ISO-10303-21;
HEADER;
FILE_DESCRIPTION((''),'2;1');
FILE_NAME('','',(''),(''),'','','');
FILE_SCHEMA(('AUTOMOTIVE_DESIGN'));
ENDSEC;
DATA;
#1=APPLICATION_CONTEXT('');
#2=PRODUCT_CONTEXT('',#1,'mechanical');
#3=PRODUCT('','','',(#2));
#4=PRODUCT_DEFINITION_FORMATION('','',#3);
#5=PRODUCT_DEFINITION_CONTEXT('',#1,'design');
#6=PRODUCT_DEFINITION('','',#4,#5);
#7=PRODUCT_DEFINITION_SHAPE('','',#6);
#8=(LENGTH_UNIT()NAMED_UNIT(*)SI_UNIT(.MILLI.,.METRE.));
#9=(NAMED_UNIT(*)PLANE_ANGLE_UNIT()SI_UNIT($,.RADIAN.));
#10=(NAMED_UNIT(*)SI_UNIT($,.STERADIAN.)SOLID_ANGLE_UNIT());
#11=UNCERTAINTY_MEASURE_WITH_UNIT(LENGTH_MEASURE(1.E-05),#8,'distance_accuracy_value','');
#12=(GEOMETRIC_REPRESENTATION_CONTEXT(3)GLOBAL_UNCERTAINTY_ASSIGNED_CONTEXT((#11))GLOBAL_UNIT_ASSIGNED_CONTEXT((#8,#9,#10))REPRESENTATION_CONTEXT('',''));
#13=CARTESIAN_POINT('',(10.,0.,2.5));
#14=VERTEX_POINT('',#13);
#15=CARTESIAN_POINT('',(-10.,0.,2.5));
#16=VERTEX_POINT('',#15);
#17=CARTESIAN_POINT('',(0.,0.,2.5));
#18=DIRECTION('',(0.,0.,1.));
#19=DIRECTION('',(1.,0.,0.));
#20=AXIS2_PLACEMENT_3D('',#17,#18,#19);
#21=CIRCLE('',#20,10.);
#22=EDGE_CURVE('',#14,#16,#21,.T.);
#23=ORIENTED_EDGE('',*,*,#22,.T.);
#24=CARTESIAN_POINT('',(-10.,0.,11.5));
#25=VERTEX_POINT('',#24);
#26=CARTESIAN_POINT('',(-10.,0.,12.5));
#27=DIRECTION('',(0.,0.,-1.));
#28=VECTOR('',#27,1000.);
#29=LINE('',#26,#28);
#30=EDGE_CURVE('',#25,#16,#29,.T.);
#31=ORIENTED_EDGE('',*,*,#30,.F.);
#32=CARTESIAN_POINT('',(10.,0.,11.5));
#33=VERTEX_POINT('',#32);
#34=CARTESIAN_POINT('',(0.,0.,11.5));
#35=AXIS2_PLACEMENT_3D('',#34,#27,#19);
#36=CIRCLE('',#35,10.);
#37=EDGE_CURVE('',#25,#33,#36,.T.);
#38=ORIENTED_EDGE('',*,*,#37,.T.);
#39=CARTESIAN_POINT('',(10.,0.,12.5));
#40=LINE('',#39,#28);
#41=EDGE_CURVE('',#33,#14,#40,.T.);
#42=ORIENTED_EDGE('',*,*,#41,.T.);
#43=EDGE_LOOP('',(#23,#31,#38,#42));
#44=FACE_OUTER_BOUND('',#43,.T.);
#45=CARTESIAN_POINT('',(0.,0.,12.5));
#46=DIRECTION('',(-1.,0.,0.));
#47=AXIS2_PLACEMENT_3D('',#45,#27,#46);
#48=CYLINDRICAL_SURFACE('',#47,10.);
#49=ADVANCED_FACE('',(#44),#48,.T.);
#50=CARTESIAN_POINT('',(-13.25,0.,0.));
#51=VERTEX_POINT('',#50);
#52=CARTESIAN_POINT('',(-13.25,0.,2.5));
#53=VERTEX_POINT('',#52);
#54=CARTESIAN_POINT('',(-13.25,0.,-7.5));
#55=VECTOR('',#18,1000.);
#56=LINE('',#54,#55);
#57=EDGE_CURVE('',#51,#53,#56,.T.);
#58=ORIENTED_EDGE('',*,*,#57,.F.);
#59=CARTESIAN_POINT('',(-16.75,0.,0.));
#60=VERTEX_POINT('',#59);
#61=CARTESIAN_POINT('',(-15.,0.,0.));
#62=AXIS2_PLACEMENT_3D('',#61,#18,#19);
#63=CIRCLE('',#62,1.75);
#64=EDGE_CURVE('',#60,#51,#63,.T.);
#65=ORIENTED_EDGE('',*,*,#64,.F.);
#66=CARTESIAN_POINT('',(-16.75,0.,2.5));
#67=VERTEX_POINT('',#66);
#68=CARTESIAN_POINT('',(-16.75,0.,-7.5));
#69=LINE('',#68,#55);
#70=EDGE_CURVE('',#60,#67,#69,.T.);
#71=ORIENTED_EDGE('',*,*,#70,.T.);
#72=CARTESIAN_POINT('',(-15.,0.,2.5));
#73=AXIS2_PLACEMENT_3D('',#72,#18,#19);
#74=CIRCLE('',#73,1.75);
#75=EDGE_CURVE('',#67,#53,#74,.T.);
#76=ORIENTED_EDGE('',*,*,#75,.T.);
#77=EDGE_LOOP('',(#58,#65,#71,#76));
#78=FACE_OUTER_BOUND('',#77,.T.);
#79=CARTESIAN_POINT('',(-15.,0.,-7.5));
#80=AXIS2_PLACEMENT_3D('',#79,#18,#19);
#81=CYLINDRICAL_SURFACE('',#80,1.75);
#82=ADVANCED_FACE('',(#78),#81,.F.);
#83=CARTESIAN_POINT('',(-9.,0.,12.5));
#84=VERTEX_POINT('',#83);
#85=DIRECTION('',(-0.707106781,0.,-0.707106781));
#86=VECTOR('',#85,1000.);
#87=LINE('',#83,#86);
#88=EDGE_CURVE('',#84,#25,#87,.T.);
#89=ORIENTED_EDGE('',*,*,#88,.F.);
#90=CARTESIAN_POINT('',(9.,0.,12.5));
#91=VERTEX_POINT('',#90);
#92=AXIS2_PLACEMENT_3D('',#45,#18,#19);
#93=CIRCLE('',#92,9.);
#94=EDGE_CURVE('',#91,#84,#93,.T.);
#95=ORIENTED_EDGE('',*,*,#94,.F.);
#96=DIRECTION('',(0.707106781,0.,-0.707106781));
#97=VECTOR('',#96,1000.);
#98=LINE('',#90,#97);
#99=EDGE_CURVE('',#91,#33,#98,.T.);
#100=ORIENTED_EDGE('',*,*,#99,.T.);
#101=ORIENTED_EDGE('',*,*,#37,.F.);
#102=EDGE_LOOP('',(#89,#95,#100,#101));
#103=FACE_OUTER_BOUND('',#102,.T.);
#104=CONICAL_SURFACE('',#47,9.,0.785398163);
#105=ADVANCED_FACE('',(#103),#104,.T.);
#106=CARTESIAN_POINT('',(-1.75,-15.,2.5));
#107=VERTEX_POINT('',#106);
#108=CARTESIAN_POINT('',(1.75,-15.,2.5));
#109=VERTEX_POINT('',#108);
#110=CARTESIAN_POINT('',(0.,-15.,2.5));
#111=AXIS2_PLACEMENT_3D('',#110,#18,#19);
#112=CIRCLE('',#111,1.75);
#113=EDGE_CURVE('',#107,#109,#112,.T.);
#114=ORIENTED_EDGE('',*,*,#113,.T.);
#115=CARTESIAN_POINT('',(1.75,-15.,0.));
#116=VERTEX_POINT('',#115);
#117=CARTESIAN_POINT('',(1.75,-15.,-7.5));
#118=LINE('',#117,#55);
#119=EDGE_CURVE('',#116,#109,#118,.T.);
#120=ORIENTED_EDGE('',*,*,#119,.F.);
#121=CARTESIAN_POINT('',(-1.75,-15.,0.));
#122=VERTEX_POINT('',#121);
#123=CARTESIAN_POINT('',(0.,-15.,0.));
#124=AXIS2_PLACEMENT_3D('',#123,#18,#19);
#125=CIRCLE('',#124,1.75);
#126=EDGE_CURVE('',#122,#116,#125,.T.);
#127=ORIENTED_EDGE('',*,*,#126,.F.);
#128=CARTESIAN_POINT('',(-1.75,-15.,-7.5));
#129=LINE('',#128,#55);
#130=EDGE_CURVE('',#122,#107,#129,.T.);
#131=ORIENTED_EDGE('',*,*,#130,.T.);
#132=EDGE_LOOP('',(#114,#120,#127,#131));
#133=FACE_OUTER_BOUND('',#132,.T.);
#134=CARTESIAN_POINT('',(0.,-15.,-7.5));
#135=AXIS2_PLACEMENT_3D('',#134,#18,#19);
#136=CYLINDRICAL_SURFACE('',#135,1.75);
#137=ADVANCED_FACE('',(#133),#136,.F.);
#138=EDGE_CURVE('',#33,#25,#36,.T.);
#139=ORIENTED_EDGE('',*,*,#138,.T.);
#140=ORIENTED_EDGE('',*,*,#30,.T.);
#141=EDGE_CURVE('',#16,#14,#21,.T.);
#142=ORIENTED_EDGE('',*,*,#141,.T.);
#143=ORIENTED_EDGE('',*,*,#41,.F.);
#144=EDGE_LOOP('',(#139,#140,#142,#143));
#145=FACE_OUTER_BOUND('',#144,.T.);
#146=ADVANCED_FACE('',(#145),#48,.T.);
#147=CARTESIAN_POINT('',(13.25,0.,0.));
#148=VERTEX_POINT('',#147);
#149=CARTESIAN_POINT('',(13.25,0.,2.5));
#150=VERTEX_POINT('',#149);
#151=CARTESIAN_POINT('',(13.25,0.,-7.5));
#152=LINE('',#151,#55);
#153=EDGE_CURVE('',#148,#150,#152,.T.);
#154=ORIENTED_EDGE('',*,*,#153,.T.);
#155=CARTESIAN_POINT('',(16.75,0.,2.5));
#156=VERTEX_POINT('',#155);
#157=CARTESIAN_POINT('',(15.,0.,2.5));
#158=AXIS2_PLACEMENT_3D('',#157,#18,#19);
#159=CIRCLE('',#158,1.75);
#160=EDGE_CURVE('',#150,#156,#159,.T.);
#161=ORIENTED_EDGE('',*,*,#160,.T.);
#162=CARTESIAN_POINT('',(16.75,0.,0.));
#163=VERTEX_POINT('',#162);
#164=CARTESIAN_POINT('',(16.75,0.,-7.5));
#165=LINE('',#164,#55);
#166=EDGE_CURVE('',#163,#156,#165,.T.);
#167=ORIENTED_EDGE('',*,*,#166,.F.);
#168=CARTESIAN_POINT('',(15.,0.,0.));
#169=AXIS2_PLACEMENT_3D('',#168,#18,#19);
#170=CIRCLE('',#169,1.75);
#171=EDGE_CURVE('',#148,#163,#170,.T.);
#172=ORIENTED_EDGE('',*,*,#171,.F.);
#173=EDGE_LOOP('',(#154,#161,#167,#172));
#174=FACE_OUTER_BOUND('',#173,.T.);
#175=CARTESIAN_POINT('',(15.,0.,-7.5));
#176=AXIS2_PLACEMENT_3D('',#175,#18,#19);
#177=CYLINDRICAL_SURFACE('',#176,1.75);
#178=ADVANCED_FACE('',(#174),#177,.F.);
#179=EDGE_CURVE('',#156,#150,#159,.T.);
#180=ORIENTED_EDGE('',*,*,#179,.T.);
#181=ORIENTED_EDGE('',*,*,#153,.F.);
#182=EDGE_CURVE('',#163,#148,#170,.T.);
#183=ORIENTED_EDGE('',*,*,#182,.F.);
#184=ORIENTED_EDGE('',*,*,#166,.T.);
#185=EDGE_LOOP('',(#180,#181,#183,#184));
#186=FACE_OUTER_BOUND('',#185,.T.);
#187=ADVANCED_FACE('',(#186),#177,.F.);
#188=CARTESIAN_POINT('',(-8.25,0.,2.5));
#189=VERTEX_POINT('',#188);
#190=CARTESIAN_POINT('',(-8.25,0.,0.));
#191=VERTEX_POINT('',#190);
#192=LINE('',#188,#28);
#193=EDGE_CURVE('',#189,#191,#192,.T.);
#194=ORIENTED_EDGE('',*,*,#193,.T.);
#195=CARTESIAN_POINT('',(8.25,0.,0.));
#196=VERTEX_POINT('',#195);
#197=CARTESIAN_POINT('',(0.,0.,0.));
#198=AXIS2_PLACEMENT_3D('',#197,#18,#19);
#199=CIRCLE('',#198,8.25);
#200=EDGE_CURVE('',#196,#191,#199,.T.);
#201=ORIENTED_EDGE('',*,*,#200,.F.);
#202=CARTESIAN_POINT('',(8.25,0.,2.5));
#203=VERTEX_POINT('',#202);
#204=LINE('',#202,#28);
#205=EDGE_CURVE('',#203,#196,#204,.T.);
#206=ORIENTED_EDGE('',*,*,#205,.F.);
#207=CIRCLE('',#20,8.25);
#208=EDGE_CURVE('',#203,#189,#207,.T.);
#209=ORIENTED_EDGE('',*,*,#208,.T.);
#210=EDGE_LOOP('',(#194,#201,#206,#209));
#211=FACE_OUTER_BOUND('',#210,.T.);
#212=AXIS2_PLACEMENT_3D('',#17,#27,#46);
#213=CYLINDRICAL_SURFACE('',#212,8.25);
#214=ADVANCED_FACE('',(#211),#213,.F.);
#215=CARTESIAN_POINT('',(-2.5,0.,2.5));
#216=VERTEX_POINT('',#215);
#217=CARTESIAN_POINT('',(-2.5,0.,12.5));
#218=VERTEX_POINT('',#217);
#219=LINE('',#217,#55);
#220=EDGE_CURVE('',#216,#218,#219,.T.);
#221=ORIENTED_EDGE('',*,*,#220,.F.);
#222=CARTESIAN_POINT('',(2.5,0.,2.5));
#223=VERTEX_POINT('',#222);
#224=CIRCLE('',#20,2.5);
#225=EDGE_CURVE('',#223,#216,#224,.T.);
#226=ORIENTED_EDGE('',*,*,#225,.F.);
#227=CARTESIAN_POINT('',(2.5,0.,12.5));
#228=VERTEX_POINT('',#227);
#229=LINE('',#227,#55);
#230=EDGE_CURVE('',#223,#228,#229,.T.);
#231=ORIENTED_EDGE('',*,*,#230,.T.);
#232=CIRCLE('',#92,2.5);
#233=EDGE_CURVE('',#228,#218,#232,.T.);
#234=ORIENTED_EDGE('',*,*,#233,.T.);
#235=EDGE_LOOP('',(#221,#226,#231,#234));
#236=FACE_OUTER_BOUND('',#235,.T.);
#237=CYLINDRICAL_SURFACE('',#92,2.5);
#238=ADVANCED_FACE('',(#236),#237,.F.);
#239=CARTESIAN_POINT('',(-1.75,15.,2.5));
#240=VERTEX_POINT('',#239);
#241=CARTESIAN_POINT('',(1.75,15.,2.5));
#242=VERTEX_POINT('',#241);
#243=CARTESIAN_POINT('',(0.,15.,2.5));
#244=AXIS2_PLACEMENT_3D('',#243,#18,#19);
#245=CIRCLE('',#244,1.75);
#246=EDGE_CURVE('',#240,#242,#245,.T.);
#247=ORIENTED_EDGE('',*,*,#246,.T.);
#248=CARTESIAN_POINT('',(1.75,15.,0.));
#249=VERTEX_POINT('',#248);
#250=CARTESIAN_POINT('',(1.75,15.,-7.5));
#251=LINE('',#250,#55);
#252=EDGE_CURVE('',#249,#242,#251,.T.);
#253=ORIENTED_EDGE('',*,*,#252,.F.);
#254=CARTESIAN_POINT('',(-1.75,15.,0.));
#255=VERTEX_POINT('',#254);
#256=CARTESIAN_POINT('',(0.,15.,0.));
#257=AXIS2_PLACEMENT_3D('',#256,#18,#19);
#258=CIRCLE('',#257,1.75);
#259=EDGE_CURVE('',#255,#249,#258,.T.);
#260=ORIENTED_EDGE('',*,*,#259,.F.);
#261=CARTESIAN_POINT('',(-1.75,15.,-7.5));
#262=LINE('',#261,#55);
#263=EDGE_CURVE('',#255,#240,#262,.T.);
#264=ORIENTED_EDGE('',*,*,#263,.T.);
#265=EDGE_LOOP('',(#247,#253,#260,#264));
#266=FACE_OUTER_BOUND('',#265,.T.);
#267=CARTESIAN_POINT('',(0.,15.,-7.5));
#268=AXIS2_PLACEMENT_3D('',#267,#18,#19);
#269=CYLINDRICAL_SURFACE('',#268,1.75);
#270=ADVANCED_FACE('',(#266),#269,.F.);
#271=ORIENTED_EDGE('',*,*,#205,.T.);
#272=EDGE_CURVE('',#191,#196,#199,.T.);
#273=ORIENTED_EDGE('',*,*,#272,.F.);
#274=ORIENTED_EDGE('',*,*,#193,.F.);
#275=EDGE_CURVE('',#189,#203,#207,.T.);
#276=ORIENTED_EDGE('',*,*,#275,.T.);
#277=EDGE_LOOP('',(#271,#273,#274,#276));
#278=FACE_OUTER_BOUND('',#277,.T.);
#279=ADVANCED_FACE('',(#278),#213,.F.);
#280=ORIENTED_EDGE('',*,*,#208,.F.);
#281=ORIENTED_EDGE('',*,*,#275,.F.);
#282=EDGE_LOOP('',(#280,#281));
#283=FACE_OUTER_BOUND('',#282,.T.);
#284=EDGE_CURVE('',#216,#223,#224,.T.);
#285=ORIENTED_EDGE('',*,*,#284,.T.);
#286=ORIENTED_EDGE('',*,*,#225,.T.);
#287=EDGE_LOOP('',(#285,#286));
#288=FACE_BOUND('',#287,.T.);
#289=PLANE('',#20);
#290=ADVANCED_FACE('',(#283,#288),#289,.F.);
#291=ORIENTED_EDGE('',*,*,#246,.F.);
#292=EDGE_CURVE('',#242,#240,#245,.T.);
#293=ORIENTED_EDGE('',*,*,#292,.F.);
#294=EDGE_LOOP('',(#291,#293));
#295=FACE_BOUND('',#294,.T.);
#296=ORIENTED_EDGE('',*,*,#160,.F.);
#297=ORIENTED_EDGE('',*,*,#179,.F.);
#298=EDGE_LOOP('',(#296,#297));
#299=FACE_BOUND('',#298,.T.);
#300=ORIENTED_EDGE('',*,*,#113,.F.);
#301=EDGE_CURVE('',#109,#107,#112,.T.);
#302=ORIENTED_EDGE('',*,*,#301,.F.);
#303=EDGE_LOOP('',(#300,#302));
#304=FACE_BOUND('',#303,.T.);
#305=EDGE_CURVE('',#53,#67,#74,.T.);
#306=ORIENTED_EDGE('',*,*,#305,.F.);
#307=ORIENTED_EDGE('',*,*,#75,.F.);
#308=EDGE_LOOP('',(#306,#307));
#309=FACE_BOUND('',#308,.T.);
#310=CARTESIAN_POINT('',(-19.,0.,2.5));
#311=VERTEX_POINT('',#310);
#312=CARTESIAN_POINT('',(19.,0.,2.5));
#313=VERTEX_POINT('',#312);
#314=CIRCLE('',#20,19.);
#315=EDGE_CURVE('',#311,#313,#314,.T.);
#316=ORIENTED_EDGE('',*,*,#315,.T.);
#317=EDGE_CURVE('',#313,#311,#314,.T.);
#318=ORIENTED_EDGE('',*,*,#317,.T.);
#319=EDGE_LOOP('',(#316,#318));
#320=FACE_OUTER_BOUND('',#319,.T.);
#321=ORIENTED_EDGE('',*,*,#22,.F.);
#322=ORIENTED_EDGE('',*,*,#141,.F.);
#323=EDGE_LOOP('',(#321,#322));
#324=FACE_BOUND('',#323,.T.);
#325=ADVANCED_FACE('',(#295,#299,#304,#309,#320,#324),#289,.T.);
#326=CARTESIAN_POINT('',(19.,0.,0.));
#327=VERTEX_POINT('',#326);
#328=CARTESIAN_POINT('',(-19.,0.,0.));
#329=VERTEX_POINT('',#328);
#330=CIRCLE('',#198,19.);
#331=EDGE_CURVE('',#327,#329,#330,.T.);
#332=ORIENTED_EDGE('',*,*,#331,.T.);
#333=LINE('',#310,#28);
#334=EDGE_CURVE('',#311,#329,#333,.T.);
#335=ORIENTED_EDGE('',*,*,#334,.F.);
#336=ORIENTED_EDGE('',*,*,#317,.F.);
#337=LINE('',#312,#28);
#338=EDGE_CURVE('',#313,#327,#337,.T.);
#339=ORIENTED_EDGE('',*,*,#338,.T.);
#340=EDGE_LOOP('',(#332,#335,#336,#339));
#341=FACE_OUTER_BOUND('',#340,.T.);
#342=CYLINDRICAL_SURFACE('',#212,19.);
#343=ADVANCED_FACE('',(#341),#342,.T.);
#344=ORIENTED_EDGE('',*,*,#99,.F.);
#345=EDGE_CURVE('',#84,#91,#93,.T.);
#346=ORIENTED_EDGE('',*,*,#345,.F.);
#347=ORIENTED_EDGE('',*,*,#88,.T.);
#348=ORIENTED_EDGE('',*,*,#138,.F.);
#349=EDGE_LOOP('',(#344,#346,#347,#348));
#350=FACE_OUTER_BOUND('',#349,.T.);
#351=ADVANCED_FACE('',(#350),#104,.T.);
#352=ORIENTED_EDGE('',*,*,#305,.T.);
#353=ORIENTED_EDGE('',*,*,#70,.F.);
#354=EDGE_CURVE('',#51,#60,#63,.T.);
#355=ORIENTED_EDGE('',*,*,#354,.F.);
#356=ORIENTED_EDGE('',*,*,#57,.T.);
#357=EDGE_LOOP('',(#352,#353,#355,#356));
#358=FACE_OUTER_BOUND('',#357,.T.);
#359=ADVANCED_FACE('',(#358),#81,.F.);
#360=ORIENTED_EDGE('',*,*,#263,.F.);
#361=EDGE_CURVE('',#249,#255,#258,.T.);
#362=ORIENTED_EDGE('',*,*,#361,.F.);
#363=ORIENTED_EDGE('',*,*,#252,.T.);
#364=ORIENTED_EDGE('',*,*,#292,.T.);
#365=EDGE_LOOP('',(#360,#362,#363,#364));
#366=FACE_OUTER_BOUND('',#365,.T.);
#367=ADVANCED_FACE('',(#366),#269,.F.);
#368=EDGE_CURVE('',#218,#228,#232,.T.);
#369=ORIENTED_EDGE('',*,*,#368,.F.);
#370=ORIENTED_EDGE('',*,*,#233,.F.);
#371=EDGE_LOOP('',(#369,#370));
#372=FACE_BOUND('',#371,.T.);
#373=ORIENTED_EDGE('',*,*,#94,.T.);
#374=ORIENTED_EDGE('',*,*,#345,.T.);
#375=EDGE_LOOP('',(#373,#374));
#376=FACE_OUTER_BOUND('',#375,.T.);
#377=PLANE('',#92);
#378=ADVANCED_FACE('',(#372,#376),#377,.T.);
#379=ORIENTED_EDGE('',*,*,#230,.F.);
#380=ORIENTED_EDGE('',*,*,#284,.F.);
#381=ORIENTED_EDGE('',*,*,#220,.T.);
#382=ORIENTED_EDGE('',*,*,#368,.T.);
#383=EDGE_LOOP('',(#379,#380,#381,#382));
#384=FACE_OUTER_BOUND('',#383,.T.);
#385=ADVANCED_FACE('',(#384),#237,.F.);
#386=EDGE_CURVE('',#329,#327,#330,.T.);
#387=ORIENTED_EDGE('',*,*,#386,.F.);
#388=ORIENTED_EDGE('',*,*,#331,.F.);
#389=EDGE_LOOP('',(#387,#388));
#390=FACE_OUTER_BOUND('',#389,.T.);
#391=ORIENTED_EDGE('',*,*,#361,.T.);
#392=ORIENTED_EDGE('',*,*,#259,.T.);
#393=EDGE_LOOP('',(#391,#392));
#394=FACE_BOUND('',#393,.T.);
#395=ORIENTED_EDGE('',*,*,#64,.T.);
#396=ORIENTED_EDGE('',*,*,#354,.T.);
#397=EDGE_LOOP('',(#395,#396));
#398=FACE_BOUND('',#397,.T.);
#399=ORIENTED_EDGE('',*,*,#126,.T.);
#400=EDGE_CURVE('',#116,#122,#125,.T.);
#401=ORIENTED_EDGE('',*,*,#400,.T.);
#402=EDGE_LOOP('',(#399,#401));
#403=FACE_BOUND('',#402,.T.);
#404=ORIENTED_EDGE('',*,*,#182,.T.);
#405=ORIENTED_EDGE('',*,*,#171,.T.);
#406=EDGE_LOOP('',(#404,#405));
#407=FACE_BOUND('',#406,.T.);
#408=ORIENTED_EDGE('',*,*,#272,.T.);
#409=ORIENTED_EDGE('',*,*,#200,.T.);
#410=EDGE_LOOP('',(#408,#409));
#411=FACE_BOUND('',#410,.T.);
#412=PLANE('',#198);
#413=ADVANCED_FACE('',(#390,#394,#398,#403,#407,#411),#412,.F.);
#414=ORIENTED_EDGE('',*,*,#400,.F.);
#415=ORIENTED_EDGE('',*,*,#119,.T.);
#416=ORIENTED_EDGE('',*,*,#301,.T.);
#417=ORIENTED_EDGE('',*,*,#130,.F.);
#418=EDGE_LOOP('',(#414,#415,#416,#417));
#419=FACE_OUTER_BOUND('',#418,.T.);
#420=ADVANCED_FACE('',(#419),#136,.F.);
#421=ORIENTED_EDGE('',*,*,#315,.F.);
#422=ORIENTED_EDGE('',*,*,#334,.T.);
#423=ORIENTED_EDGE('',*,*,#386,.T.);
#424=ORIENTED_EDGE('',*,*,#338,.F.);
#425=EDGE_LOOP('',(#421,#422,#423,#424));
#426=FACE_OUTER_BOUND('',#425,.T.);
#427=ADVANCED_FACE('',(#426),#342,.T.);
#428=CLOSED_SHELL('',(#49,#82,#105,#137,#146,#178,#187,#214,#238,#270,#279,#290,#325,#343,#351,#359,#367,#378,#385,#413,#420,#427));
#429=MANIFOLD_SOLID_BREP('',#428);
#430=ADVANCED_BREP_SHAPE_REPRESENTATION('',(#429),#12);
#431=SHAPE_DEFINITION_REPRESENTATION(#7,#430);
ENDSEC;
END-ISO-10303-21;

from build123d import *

# Parameters (mm, degrees)
SKETCH1_R           = 19
SKETCH1_R_2         = 8.25
BOSS_EXTRUDE1_DEPTH = 2.5
SKETCH2_R           = 10
BOSS_EXTRUDE2_DEPTH = 10
SKETCH3_R           = 1.75
CUT_EXTRUDE1_DEPTH  = 10
CHAMFER1_SIZE       = 1
M6_TAPPED_HOLE1_D   = 5


with BuildPart() as part:
    # Sketch1 → Boss-Extrude1 (new body)
    with BuildSketch(Plane.XY):
        Circle(SKETCH1_R)
        Circle(SKETCH1_R_2, mode=Mode.SUBTRACT)
    extrude(amount=BOSS_EXTRUDE1_DEPTH)

    # Sketch2 → Boss-Extrude2 (add)
    with BuildSketch(Plane.XY.offset(2.5)):
        Circle(SKETCH2_R)
    extrude(amount=BOSS_EXTRUDE2_DEPTH)

    # Sketch3 → Cut-Extrude1 (cut)
    with BuildSketch(Plane.XY.offset(2.5)):
        with Locations((15, 0)):
            Circle(SKETCH3_R)
        with Locations((0, 15)):
            Circle(SKETCH3_R)
        with Locations((-15, 0)):
            Circle(SKETCH3_R)
        with Locations((0, -15)):
            Circle(SKETCH3_R)
    extrude(amount=-CUT_EXTRUDE1_DEPTH, mode=Mode.SUBTRACT)

    # Chamfer1
    chamfer1_edges = [part.edges().sort_by_distance(p)[0] for p in [
        (-10, 0, 12.5),
    ]]
    chamfer(chamfer1_edges, length=CHAMFER1_SIZE)

    # M6 Tapped Hole1 (through all)
    with Locations(Plane.XY.offset(12.5)):
        with Locations((0, 0)):
            Hole(M6_TAPPED_HOLE1_D / 2)


solid = part.part
